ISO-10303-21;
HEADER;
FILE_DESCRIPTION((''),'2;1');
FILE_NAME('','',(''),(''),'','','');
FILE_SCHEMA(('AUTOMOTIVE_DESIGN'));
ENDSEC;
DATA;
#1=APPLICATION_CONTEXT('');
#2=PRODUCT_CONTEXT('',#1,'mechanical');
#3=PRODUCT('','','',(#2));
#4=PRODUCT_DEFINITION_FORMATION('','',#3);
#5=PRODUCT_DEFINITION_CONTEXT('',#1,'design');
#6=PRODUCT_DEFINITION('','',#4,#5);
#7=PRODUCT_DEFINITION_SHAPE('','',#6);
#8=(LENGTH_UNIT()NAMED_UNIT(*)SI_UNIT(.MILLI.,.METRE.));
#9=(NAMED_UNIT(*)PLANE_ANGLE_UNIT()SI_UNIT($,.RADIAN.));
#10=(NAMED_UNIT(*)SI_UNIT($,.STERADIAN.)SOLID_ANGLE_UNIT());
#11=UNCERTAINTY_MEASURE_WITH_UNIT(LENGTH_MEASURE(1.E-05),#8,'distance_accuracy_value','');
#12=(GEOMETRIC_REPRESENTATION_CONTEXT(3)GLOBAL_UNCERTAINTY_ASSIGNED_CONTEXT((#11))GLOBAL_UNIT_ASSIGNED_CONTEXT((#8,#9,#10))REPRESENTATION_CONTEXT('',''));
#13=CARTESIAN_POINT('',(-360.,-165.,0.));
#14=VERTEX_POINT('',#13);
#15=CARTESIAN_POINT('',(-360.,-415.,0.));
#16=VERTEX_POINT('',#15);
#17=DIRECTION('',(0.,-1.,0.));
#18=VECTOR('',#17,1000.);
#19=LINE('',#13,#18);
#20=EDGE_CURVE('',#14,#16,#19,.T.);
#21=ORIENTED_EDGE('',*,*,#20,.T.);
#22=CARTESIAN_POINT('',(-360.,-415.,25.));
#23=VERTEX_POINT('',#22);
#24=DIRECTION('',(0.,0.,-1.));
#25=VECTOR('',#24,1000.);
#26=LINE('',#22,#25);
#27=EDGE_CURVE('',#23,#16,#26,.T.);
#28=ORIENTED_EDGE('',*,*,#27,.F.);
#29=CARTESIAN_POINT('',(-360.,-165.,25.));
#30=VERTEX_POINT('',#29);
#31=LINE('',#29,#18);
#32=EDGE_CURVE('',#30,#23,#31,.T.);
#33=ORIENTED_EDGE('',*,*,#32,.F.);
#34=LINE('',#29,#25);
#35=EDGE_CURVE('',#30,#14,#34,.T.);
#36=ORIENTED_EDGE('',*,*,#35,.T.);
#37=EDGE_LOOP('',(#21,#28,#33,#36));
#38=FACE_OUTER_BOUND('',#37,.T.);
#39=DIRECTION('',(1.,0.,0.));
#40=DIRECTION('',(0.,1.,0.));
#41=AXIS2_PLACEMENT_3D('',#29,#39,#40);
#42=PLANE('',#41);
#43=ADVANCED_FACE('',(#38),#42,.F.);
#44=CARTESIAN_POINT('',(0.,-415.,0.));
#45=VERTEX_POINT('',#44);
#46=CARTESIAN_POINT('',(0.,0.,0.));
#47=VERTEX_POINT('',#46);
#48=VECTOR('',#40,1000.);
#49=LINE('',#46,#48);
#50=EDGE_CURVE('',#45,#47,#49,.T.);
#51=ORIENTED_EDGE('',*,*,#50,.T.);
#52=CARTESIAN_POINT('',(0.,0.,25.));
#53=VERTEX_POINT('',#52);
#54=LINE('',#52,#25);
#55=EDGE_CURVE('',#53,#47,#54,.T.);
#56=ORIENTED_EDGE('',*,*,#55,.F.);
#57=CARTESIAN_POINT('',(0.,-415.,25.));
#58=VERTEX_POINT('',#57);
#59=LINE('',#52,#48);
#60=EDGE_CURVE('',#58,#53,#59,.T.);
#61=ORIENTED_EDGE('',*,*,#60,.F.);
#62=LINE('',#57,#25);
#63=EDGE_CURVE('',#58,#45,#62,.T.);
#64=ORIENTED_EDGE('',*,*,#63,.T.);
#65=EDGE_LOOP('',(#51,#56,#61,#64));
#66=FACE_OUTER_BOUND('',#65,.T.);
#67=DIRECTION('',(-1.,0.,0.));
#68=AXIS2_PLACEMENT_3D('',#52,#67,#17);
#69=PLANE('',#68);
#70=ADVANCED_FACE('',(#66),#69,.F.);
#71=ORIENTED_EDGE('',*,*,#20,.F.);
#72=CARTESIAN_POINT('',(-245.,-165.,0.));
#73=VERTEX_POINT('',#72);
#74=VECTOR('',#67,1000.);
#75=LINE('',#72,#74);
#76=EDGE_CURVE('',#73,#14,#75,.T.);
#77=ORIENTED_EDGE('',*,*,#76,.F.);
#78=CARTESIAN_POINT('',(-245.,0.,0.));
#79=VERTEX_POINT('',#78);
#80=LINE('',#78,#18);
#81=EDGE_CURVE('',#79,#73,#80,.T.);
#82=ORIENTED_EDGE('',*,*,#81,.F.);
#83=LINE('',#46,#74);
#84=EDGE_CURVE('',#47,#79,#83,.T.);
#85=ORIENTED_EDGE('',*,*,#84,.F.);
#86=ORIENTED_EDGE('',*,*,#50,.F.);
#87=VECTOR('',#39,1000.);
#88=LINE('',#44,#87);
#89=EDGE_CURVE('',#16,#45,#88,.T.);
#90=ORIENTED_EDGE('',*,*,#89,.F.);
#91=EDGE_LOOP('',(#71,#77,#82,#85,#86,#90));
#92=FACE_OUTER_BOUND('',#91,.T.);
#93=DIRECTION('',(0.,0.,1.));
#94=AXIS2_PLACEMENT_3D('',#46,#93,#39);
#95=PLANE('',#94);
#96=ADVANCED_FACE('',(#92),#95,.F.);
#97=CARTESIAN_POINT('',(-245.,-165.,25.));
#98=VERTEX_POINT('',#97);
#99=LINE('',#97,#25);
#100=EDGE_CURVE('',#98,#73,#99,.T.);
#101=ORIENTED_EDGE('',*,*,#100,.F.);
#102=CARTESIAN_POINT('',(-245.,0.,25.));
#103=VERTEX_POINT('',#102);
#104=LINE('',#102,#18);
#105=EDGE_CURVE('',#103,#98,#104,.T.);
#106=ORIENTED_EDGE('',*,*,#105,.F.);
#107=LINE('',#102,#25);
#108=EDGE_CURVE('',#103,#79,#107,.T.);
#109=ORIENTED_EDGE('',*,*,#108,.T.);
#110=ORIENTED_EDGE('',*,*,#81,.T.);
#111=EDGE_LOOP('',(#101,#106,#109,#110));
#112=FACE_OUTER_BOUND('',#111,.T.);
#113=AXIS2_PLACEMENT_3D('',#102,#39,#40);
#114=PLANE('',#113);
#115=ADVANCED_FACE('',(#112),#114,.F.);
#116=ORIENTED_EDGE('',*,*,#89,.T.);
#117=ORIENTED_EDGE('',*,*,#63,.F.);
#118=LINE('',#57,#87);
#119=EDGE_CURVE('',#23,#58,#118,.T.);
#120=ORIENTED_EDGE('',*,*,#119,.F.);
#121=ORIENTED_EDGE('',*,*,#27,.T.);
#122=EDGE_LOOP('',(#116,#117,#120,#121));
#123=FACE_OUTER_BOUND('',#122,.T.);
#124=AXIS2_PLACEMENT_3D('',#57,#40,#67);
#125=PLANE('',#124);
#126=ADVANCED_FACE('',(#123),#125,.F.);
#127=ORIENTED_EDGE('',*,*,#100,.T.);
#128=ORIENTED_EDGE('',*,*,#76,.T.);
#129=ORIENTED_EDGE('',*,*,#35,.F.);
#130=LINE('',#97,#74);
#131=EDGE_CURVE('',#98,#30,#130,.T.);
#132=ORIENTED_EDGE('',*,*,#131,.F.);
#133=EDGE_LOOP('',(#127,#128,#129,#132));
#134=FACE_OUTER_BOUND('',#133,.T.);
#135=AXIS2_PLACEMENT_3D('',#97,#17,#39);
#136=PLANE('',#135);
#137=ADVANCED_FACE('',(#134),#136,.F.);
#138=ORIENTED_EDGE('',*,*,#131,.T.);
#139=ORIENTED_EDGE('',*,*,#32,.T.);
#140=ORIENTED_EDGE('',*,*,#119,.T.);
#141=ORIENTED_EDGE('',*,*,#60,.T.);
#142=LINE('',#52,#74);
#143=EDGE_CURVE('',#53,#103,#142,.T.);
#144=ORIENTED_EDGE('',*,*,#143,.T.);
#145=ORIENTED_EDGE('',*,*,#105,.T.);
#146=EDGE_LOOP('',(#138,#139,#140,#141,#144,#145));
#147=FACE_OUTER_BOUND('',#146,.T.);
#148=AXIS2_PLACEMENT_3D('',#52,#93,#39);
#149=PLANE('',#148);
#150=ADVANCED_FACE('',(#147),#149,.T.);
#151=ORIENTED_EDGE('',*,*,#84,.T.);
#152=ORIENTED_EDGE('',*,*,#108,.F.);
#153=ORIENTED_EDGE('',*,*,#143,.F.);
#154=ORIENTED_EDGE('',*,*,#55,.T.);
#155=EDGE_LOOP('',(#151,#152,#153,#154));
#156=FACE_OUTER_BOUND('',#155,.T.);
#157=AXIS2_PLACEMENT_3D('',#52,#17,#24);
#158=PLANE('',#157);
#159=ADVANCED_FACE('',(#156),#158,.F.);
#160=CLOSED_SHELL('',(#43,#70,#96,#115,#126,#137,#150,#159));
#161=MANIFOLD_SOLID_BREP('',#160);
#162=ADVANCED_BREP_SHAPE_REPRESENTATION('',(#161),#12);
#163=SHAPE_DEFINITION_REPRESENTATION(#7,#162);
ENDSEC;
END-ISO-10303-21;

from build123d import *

# Parameters (mm, degrees)
BOSS_EXTRUDE1_DEPTH = 25


with BuildPart() as part:
    # Sketch1 → Boss-Extrude1 (new body)
    with BuildSketch(Plane.XY):
        Polygon((0, 0), (0, -415), (-360, -415), (-360, -165), (-245, -165), (-245, 0), align=None)
    extrude(amount=BOSS_EXTRUDE1_DEPTH)


solid = part.part
